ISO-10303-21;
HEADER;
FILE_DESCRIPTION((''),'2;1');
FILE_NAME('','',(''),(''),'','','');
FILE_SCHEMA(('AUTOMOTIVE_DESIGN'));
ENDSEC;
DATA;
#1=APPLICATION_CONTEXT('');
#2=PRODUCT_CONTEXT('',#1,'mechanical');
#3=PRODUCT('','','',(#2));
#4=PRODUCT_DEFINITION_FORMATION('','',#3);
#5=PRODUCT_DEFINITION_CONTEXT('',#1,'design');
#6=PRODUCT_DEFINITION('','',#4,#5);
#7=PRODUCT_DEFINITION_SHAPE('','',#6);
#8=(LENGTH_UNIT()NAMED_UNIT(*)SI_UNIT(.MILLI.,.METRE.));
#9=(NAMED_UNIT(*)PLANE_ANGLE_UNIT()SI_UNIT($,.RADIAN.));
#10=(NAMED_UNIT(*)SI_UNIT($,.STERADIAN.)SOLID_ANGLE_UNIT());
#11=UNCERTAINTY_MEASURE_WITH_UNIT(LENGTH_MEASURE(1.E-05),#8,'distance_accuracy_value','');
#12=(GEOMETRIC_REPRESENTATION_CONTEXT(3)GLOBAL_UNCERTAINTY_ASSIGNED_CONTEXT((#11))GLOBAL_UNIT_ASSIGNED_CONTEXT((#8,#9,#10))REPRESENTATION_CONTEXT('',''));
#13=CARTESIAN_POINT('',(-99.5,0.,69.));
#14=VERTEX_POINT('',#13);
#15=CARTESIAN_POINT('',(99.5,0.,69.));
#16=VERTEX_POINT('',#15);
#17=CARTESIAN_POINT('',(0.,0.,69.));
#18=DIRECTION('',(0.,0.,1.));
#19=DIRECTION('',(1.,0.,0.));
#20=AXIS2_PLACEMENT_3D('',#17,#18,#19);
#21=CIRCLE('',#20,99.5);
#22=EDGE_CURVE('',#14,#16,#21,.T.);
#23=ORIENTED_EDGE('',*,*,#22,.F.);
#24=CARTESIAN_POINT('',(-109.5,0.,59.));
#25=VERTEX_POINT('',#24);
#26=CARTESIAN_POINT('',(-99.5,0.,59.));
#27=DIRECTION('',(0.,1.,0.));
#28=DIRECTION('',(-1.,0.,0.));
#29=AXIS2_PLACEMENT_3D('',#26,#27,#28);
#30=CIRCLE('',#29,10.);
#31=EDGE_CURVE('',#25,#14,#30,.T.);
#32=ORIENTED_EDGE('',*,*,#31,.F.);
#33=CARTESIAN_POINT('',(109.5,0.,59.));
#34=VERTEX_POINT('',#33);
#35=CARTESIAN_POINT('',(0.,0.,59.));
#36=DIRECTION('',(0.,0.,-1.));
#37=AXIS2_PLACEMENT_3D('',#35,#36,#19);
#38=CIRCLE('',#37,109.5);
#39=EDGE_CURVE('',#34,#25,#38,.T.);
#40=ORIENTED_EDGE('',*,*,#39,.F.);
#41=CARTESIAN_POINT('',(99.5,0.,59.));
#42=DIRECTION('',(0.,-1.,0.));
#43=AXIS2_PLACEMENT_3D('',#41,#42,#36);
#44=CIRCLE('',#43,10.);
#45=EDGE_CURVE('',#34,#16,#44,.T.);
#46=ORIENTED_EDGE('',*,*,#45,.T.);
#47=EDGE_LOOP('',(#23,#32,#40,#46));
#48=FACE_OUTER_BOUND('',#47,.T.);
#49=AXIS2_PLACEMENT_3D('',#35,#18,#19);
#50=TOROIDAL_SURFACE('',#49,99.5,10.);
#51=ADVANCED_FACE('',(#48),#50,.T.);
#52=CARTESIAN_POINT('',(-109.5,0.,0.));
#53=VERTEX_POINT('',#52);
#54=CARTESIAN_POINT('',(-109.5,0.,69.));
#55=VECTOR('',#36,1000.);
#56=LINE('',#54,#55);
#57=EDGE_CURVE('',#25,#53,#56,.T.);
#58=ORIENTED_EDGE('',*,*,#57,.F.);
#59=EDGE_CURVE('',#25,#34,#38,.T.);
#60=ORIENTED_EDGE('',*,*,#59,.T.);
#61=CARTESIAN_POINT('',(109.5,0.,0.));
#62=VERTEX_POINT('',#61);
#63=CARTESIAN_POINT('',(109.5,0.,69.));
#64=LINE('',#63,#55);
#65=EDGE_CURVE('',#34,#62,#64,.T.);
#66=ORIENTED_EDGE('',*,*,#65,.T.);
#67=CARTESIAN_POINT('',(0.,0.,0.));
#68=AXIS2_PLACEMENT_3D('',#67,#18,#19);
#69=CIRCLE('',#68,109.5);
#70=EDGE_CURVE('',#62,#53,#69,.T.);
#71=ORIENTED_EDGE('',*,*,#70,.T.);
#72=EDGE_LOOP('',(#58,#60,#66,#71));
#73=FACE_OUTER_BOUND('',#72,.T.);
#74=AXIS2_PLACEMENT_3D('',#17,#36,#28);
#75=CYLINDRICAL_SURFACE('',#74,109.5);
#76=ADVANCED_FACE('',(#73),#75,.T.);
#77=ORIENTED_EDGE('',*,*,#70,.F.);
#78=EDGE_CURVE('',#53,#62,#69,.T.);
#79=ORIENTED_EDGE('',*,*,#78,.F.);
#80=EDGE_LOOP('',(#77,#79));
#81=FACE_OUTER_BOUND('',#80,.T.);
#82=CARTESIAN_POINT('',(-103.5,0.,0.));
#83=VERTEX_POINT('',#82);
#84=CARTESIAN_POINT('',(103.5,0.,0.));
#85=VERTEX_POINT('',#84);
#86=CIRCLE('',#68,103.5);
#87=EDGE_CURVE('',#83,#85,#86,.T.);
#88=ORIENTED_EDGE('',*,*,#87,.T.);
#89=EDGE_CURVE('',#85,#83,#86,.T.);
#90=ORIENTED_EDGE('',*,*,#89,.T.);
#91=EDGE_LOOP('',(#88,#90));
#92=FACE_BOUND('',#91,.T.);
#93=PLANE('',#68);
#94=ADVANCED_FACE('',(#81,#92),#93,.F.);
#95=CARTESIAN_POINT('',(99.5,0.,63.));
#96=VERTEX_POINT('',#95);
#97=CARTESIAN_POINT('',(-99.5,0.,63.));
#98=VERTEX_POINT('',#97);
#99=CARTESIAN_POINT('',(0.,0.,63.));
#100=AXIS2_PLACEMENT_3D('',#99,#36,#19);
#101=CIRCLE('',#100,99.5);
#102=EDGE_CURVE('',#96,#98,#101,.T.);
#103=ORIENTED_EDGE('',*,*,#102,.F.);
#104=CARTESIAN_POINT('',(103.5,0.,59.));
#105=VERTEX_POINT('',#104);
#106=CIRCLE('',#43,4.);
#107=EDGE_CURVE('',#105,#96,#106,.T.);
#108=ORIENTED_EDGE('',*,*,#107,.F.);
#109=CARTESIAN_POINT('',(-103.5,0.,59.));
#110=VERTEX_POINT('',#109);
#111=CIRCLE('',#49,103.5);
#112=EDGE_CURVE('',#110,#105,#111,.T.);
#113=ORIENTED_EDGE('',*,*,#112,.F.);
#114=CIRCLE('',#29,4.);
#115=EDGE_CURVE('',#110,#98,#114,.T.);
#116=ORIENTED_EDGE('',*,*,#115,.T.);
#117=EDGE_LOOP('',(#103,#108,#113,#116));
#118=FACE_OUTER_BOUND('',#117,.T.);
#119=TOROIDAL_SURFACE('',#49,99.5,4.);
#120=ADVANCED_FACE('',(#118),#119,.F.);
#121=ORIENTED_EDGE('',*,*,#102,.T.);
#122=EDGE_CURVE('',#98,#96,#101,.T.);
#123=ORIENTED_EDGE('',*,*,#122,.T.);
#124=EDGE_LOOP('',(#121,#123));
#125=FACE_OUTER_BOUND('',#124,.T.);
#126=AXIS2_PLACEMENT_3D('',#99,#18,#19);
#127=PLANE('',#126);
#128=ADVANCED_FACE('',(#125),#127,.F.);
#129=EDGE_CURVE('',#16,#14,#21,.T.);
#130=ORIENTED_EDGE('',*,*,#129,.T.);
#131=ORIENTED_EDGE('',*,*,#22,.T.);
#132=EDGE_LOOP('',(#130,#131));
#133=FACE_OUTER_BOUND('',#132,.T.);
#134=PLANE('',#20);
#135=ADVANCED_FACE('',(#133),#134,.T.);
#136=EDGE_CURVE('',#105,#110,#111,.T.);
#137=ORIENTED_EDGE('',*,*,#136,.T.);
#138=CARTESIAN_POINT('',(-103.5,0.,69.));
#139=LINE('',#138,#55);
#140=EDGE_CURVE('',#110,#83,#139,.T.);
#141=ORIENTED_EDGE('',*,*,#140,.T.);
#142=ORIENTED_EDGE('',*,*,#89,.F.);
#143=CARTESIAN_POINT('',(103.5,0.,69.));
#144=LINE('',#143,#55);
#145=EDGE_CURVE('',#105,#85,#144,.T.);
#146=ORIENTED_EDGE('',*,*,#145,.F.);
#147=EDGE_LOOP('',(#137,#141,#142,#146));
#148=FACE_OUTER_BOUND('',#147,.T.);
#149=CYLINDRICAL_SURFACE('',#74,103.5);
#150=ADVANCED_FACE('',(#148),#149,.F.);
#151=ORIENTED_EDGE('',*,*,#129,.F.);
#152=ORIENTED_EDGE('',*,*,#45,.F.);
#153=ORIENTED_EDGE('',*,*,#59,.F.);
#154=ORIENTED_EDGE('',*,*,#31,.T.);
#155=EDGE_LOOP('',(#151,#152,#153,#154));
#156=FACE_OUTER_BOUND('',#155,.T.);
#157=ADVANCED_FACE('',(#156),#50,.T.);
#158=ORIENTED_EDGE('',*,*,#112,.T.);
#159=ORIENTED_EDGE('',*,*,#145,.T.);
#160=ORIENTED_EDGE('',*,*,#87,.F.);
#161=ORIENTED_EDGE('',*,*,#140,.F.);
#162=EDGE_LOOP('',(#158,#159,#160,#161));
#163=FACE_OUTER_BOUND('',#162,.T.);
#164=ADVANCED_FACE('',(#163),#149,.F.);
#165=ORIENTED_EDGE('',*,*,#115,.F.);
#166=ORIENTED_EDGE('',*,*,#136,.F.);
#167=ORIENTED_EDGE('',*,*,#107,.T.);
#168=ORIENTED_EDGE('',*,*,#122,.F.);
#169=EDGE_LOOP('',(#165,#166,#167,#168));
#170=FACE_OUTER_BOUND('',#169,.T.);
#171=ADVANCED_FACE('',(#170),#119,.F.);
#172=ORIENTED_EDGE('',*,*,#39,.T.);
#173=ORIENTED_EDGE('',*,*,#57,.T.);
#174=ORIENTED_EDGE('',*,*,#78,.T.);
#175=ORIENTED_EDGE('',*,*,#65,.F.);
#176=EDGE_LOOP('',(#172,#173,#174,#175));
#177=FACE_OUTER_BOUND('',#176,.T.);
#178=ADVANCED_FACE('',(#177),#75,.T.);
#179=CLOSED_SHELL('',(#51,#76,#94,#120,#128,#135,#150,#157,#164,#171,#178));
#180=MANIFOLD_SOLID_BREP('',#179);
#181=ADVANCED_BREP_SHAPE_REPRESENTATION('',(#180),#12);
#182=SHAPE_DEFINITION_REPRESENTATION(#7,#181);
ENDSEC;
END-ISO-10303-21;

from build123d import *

# Parameters (mm, degrees)
SKETCH1_R           = 109.5
BOSS_EXTRUDE1_DEPTH = 69
SHELL1_T            = -6
FILLET1_R           = 10
FILLET2_R           = 4


with BuildPart() as part:
    # Sketch1 → Boss-Extrude1 (new body)
    with BuildSketch(Plane.XY):
        Circle(SKETCH1_R)
    extrude(amount=BOSS_EXTRUDE1_DEPTH)

    # Shell1
    shell1_openings = [part.faces().sort_by_distance(p)[0] for p in [
        (0, 0, 0),
    ]]
    offset(amount=SHELL1_T, openings=shell1_openings, kind=Kind.INTERSECTION)

    # Fillet1
    fillet1_edges = [part.edges().sort_by_distance(p)[0] for p in [
        (-109.5, 0, 69),
    ]]
    fillet(fillet1_edges, radius=FILLET1_R)

    # Fillet2
    fillet2_edges = [part.edges().sort_by_distance(p)[0] for p in [
        (-103.5, 0, 63),
    ]]
    fillet(fillet2_edges, radius=FILLET2_R)


solid = part.part
